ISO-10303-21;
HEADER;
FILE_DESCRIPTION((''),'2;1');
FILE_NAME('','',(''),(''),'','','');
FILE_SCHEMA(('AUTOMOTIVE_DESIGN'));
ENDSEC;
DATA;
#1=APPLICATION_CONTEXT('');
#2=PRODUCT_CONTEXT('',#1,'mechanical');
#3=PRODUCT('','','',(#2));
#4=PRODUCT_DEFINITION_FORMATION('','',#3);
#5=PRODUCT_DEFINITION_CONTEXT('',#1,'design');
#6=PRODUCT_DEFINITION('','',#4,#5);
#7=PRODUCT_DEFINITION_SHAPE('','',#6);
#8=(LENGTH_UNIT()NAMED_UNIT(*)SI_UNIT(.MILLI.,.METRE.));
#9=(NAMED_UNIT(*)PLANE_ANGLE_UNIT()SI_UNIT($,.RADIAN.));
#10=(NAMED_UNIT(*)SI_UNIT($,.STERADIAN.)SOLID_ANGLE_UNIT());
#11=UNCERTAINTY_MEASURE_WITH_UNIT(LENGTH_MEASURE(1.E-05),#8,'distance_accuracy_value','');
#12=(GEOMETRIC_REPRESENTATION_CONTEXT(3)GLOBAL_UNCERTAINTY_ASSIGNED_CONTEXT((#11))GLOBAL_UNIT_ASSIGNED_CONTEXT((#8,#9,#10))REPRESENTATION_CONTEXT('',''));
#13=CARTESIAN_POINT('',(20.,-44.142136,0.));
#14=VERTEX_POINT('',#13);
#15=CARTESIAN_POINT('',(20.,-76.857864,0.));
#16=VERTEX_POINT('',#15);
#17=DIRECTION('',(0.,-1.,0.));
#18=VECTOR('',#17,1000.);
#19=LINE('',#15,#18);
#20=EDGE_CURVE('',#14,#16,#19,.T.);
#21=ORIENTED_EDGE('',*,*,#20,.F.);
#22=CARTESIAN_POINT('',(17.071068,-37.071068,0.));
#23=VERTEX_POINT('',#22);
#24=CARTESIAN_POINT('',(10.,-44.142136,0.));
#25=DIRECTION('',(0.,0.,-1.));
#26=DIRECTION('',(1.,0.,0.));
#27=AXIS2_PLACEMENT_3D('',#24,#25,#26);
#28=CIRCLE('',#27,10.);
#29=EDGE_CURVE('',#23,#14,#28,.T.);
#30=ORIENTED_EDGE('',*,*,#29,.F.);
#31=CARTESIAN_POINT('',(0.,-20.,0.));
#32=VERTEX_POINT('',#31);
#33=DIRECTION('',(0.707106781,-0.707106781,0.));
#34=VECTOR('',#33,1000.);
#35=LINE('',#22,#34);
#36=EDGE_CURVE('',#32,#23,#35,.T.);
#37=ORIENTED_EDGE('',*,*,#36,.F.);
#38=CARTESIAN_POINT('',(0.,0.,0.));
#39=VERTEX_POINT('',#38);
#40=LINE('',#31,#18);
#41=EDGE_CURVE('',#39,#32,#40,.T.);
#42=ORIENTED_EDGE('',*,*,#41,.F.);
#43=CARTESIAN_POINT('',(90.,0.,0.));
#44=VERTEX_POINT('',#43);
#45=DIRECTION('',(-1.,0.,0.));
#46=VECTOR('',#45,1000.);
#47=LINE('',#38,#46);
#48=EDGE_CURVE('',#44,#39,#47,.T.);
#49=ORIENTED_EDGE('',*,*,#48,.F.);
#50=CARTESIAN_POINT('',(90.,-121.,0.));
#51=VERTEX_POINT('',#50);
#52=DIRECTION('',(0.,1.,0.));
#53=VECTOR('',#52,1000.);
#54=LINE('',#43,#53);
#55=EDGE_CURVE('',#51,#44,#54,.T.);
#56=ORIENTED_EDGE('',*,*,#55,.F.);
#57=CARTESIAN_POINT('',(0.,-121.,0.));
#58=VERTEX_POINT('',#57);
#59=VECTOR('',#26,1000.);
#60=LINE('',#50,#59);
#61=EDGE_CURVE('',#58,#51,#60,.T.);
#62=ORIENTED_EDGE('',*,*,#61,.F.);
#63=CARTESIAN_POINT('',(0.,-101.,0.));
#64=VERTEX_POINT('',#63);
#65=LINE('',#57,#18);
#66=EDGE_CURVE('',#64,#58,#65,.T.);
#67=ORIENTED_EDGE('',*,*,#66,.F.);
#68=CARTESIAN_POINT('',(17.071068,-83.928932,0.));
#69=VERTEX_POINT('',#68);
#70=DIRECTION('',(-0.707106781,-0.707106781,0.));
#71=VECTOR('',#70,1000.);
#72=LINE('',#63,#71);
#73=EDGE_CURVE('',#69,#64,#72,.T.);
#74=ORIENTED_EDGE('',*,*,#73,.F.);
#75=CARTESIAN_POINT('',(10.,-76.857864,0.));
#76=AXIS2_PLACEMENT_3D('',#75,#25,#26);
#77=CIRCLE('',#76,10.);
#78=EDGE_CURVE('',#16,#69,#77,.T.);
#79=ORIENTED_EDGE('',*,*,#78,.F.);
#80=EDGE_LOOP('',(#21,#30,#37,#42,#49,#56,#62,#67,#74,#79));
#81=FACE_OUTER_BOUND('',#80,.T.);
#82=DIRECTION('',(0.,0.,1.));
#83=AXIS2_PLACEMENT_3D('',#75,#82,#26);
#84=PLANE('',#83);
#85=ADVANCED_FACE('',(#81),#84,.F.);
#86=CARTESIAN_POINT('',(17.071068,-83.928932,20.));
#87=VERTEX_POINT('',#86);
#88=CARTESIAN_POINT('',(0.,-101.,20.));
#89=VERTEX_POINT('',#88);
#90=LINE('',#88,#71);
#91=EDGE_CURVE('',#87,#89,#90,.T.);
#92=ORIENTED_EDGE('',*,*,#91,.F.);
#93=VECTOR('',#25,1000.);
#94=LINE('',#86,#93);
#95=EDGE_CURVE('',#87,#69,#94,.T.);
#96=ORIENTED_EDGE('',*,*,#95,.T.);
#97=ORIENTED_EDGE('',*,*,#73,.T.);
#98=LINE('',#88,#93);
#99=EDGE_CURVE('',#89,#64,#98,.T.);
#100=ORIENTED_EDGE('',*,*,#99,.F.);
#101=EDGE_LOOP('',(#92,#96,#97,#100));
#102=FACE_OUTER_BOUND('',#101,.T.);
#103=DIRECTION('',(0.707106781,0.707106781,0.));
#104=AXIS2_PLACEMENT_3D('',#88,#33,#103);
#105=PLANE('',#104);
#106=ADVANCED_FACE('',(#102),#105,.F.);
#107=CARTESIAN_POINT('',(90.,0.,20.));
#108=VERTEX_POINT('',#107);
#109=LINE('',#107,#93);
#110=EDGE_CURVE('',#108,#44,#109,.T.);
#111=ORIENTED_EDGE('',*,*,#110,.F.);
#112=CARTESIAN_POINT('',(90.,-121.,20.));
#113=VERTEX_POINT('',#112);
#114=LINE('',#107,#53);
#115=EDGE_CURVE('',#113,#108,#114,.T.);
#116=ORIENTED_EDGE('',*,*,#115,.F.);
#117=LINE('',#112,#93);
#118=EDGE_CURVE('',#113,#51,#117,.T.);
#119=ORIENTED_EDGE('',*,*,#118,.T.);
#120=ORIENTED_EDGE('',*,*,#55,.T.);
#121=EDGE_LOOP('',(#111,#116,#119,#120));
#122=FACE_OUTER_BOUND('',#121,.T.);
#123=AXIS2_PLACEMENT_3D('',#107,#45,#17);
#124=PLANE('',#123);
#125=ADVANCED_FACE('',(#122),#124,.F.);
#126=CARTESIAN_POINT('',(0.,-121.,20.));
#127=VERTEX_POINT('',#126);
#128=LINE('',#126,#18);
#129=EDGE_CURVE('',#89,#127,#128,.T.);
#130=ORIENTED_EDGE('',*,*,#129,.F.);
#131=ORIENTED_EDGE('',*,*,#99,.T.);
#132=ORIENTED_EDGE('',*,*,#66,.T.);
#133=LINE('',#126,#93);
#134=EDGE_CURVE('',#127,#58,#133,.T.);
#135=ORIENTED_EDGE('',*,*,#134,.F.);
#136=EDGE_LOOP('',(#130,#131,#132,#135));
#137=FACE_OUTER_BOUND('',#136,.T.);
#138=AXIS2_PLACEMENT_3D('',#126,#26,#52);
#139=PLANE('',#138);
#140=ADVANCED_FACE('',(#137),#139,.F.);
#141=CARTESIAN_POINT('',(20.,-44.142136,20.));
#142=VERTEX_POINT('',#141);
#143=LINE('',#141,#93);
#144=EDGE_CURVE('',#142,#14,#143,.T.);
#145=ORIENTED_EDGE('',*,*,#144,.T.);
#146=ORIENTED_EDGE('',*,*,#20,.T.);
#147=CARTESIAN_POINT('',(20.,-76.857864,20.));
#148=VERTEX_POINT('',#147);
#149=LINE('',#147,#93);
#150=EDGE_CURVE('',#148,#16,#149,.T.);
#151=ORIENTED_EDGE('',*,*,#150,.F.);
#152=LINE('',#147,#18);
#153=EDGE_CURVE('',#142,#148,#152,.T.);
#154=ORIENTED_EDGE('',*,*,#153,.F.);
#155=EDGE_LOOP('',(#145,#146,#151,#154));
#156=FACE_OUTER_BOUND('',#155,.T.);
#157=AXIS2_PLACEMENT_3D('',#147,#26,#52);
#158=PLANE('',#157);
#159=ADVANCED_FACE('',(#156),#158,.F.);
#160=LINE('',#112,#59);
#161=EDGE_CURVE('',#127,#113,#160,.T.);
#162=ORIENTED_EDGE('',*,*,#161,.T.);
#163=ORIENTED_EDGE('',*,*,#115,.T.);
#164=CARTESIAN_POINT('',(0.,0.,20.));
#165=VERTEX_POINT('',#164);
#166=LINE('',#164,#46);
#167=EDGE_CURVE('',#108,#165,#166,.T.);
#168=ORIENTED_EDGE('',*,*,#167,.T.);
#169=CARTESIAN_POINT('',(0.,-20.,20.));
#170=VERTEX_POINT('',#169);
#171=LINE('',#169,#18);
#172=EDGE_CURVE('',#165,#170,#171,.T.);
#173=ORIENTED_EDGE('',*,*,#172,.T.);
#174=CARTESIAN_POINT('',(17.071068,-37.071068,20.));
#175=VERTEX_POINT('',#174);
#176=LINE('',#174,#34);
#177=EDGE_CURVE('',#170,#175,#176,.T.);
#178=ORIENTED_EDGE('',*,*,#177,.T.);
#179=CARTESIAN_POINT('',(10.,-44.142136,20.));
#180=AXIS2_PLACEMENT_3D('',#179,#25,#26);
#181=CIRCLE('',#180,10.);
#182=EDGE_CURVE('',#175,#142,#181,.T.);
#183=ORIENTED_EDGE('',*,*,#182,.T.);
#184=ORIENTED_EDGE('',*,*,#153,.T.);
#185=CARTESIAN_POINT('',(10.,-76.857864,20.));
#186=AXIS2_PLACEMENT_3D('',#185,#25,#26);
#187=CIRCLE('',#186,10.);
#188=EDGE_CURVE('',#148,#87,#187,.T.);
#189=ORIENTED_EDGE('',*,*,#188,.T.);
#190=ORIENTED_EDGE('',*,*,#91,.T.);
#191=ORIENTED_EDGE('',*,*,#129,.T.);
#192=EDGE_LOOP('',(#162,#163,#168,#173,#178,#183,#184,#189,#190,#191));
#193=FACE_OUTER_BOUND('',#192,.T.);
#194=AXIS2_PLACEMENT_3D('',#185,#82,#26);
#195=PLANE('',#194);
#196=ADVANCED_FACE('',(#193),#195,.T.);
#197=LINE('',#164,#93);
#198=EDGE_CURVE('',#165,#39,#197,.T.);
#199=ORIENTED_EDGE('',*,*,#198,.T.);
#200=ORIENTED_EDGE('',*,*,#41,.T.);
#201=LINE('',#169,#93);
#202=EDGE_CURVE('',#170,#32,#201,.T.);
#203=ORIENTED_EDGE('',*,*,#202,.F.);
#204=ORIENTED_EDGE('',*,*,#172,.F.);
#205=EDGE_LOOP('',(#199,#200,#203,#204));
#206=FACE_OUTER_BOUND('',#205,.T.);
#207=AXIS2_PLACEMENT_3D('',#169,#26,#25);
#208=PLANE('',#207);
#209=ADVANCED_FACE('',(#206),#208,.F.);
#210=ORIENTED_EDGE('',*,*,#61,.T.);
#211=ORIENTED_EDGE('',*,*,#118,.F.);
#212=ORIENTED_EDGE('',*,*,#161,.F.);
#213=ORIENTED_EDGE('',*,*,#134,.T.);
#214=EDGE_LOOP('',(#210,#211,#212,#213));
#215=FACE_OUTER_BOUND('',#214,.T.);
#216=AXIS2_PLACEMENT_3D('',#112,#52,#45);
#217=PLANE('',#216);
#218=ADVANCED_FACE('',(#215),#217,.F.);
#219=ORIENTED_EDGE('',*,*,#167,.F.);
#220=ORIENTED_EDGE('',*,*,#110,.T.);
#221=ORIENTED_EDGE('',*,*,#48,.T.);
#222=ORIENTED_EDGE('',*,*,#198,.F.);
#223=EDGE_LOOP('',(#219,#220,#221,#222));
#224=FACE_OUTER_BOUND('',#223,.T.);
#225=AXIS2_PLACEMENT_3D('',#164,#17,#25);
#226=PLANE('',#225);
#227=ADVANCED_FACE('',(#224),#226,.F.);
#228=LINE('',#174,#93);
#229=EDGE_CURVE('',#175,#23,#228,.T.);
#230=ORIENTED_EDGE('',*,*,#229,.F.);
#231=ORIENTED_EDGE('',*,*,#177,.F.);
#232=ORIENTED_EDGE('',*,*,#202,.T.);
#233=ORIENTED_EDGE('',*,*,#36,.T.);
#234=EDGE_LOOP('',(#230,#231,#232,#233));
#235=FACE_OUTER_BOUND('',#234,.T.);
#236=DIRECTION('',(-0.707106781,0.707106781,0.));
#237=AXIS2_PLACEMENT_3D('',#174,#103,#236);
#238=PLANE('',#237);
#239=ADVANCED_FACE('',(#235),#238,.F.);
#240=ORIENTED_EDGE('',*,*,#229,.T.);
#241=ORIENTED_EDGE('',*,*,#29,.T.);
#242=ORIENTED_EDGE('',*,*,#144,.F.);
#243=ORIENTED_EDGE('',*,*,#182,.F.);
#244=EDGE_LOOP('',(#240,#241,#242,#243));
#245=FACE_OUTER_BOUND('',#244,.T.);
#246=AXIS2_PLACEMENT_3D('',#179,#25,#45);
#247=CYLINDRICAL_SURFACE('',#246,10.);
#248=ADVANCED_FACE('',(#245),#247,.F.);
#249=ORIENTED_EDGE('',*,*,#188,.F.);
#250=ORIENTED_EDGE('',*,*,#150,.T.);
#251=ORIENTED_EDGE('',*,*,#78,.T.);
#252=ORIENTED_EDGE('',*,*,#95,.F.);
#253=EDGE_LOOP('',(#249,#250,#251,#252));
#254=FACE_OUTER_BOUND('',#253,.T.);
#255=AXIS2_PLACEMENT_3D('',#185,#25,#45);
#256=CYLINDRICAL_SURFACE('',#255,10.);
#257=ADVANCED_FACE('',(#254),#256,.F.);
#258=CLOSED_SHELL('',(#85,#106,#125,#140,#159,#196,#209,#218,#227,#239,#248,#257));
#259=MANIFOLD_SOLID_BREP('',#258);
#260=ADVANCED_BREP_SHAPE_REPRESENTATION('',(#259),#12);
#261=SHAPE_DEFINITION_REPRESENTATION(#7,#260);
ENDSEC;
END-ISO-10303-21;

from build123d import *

# Parameters (mm, degrees)
BOSS_EXTRUDE1_DEPTH = 20


with BuildPart() as part:
    # Sketch1 → Boss-Extrude1 (new body)
    with BuildSketch(Plane.XY):
        with BuildLine():
            Line((0, 0), (90, 0))
            Line((90, 0), (90, -121))
            Line((90, -121), (0, -121))
            Line((0, -121), (0, -101))
            Line((0, -101), (17.071067812, -83.928932188))
            ThreePointArc((17.071067812, -83.928932188), (19.238795325, -80.6846987), (20, -76.857864376))
            Line((20, -76.857864376), (20, -44.142135624))
            ThreePointArc((20, -44.142135624), (19.238795325, -40.3153013), (17.071067812, -37.071067812))
            Line((17.071067812, -37.071067812), (0, -20))
            Line((0, -20), (0, 0))
        make_face()
    extrude(amount=BOSS_EXTRUDE1_DEPTH)


solid = part.part
